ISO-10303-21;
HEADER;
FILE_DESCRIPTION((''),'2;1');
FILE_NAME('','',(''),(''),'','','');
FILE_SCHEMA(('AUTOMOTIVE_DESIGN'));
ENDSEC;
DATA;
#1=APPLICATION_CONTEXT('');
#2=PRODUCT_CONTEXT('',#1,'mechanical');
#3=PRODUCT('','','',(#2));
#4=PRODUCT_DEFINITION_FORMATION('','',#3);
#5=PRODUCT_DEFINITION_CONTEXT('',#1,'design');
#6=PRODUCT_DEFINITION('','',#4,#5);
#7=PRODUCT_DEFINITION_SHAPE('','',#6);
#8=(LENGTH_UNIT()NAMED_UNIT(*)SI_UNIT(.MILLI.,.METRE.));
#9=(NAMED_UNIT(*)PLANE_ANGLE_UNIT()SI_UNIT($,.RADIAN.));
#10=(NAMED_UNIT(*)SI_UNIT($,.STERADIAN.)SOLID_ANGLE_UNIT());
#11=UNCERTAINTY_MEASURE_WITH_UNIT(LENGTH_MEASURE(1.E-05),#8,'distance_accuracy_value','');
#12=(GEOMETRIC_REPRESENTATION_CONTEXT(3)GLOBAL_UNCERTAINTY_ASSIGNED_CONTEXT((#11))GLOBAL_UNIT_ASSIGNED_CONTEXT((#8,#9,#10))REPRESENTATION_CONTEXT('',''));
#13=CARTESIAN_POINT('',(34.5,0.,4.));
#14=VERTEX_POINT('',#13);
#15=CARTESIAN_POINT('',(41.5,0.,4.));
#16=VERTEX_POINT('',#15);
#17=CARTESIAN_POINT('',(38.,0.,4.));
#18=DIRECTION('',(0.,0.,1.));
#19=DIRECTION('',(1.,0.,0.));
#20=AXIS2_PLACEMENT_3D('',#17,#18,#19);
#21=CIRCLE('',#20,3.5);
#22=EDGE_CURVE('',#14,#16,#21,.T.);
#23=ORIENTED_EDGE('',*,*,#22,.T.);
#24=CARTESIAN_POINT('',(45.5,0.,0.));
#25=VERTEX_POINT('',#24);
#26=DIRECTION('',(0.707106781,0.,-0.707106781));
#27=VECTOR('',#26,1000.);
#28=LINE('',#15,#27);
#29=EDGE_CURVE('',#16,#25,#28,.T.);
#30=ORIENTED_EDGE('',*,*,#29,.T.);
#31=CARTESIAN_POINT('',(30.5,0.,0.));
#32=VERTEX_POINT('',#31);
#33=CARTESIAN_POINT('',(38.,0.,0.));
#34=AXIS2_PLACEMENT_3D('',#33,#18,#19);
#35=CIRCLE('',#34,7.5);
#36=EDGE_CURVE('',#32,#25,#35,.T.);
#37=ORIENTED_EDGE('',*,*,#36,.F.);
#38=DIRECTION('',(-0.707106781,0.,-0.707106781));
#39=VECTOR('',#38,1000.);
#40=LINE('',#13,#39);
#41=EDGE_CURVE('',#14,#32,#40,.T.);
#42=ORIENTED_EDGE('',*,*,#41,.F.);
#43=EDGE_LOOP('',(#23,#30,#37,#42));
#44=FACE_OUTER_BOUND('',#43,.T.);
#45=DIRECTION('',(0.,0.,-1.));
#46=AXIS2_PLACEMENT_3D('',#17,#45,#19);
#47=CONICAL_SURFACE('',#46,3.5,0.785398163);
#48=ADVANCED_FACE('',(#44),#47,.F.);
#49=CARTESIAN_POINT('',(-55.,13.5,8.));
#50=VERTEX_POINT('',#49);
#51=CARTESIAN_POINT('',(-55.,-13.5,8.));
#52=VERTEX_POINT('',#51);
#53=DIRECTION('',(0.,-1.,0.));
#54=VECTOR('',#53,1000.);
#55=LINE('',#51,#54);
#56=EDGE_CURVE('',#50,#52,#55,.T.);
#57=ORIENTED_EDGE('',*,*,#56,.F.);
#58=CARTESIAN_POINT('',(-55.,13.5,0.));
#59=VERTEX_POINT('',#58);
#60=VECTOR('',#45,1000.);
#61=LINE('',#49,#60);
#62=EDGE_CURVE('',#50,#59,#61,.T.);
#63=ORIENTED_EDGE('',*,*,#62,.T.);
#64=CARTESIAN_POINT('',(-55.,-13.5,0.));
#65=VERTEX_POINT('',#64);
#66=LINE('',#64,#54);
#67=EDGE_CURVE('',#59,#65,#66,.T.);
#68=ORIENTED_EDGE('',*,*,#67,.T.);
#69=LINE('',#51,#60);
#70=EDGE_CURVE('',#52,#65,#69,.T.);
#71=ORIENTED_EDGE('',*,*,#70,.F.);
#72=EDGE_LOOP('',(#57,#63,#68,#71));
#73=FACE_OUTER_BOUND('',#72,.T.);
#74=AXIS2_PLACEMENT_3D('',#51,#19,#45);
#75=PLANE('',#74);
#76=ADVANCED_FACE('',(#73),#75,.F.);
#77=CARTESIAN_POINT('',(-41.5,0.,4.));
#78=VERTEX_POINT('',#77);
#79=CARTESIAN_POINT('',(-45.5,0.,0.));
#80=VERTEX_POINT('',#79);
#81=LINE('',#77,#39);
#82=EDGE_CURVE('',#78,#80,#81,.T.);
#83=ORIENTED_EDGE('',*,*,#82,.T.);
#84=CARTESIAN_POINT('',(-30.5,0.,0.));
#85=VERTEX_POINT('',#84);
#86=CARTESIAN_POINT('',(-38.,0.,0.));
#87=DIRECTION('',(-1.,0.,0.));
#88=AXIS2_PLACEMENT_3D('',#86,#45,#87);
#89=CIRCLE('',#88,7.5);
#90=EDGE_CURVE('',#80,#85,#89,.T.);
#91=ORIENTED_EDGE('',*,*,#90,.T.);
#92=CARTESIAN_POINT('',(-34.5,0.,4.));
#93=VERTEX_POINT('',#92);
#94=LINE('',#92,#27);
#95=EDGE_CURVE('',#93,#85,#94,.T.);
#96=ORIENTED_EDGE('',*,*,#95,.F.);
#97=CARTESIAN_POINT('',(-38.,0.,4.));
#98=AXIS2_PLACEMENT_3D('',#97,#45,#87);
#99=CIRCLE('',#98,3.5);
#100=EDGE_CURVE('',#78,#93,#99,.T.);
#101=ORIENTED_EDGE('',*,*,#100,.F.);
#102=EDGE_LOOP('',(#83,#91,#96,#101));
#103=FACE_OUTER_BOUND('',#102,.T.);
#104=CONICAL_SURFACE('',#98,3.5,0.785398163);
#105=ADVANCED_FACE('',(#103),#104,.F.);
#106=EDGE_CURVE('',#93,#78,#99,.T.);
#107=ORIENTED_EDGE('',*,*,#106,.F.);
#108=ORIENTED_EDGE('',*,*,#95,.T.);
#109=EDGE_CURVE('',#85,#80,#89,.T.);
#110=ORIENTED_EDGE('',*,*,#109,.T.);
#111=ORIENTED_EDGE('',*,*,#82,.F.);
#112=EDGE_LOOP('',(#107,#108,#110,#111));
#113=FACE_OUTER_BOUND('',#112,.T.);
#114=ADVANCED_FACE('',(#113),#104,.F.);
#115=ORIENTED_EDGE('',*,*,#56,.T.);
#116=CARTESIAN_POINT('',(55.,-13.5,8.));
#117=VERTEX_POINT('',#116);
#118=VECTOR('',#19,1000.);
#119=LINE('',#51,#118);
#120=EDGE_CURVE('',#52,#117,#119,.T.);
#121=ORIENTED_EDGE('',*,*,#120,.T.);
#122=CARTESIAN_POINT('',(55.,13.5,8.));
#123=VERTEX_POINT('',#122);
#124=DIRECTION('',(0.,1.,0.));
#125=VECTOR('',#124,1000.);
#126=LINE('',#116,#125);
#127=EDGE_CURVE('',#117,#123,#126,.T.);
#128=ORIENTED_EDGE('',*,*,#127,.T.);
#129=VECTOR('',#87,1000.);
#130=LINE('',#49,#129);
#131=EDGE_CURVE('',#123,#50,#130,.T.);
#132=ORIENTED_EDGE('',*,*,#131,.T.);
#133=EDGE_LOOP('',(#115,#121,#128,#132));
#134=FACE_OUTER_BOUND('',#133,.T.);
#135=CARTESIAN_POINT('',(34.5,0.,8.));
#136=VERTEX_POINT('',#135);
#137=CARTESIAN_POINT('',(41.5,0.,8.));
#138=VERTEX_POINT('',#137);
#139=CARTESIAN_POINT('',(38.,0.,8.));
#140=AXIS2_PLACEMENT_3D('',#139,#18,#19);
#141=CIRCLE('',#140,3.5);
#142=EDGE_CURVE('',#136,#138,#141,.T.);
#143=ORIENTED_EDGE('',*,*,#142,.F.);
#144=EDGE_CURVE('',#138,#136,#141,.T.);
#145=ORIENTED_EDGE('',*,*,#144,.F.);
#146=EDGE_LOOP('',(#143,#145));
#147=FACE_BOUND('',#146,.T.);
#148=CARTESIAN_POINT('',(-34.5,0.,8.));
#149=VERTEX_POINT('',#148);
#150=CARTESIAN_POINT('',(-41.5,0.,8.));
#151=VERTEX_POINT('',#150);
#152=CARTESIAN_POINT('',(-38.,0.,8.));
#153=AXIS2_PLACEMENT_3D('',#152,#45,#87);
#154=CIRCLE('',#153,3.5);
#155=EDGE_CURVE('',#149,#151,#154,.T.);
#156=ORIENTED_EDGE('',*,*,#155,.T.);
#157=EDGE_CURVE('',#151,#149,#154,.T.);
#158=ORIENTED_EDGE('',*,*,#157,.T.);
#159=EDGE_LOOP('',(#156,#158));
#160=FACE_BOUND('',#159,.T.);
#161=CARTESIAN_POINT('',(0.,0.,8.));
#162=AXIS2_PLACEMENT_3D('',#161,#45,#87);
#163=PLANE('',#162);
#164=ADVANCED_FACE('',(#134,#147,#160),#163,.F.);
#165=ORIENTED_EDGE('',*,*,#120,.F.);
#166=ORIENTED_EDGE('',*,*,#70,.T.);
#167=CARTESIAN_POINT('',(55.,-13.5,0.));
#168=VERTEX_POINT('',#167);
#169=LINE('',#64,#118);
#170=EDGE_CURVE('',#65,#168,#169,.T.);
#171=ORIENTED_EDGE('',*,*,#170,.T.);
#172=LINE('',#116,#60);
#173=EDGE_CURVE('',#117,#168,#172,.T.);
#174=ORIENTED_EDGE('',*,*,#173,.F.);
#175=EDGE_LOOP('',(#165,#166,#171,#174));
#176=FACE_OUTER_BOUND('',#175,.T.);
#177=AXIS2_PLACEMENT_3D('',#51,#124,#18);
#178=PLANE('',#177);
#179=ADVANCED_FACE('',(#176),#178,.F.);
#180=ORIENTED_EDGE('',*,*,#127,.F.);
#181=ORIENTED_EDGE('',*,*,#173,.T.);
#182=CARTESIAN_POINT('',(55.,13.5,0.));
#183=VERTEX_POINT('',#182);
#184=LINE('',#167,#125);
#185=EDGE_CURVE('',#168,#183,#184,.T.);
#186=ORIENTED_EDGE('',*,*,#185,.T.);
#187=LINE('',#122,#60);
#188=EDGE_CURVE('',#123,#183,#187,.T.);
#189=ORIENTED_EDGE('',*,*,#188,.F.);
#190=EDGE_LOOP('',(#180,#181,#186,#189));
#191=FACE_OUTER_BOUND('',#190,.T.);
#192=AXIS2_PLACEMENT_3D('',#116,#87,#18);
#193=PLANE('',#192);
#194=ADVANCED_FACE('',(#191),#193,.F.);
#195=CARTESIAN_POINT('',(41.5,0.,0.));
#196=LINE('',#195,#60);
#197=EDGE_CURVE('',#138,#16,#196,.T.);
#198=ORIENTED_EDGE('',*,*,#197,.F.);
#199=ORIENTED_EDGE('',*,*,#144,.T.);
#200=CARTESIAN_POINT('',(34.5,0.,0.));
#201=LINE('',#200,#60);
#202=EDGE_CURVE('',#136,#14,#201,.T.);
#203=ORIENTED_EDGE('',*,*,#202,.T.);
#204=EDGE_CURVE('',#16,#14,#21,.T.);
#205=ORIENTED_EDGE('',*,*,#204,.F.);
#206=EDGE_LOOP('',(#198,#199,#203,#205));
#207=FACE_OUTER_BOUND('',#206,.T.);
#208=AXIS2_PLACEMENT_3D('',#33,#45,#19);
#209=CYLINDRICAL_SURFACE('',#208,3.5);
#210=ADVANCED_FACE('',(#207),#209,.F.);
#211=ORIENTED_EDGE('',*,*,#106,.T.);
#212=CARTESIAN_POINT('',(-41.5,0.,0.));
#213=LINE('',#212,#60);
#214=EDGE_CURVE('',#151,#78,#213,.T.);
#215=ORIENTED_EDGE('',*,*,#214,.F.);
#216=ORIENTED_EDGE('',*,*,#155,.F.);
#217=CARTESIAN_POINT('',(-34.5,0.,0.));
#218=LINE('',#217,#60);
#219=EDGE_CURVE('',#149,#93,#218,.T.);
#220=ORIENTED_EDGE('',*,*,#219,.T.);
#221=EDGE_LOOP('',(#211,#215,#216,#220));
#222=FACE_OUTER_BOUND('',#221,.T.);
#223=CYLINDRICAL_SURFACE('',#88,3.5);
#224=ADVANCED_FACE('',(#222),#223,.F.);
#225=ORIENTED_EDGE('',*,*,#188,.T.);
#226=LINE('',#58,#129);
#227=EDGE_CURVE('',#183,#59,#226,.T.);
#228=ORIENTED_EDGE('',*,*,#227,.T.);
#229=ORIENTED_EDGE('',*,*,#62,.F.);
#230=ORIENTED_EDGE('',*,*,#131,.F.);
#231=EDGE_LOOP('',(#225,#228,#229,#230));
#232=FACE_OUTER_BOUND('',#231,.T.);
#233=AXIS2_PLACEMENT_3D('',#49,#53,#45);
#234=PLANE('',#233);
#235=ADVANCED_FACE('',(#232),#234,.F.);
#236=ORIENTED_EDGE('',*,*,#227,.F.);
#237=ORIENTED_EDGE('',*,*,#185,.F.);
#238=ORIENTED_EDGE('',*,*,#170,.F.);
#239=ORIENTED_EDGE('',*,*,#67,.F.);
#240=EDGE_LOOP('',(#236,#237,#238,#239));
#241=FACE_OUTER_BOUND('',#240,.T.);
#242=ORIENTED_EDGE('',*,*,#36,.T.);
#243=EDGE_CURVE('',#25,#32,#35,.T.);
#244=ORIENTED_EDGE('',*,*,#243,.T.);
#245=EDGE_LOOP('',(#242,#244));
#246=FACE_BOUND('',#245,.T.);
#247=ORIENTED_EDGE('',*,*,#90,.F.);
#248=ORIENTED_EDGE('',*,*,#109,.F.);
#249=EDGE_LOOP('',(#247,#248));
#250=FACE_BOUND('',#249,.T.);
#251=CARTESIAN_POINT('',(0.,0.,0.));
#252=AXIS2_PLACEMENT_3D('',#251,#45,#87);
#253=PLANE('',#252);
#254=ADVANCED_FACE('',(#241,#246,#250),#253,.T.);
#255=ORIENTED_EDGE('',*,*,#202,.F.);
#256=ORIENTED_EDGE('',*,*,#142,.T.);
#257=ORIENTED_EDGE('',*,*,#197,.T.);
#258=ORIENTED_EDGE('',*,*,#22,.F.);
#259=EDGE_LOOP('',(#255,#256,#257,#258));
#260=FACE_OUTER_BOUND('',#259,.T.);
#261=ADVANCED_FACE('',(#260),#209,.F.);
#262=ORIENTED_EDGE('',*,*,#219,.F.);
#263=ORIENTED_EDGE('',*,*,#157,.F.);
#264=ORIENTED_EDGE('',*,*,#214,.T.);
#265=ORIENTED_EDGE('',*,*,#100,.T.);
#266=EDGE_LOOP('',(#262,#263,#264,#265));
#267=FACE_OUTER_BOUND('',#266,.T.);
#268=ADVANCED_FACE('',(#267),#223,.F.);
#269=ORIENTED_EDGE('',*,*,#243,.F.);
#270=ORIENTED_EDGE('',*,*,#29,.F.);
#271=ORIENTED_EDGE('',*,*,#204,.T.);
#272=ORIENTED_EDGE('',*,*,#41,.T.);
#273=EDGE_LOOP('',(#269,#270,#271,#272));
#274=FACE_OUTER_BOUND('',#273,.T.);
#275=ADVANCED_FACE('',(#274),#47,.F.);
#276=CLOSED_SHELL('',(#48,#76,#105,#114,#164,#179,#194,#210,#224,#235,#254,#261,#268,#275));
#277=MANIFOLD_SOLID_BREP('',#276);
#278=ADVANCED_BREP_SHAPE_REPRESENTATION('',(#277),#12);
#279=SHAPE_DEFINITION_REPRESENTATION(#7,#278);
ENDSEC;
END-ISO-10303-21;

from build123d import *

# Parameters (mm, degrees)
SKETCH1_W           = 110
SKETCH1_H           = 27
BOSS_EXTRUDE1_DEPTH = 8


with BuildPart() as part:
    # Sketch1 → Boss-Extrude1 (new body)
    with BuildSketch(Plane.XY):
        Rectangle(SKETCH1_W, SKETCH1_H)
    extrude(amount=BOSS_EXTRUDE1_DEPTH)

    # Sketch2 → Cut-Revolve2 (revolve, cut)
    with BuildSketch(Plane(origin=(0, 0, 0), x_dir=(1, 0, 0), z_dir=(0, 1, 0)), mode=Mode.PRIVATE) as cut_revolve2_sk:
        Polygon((-30.5, 0), (-34.5, -4), (-34.5, -8), (-38, -8), (-38, 0), align=None)
    cut_revolve2 = revolve(cut_revolve2_sk.sketch.rotate(Axis((-38, 0, 0), (0, 0, 1)), 180), axis=Axis((-38, 0, 0), (0, 0, 1)), mode=Mode.SUBTRACT)

    # Mirror1: Cut-Revolve2 across plane
    add(cut_revolve2.mirror(Plane(origin=(0, 0, 0), x_dir=(0, 0, 1), z_dir=(1, 0, 0))), mode=Mode.SUBTRACT)


solid = part.part
